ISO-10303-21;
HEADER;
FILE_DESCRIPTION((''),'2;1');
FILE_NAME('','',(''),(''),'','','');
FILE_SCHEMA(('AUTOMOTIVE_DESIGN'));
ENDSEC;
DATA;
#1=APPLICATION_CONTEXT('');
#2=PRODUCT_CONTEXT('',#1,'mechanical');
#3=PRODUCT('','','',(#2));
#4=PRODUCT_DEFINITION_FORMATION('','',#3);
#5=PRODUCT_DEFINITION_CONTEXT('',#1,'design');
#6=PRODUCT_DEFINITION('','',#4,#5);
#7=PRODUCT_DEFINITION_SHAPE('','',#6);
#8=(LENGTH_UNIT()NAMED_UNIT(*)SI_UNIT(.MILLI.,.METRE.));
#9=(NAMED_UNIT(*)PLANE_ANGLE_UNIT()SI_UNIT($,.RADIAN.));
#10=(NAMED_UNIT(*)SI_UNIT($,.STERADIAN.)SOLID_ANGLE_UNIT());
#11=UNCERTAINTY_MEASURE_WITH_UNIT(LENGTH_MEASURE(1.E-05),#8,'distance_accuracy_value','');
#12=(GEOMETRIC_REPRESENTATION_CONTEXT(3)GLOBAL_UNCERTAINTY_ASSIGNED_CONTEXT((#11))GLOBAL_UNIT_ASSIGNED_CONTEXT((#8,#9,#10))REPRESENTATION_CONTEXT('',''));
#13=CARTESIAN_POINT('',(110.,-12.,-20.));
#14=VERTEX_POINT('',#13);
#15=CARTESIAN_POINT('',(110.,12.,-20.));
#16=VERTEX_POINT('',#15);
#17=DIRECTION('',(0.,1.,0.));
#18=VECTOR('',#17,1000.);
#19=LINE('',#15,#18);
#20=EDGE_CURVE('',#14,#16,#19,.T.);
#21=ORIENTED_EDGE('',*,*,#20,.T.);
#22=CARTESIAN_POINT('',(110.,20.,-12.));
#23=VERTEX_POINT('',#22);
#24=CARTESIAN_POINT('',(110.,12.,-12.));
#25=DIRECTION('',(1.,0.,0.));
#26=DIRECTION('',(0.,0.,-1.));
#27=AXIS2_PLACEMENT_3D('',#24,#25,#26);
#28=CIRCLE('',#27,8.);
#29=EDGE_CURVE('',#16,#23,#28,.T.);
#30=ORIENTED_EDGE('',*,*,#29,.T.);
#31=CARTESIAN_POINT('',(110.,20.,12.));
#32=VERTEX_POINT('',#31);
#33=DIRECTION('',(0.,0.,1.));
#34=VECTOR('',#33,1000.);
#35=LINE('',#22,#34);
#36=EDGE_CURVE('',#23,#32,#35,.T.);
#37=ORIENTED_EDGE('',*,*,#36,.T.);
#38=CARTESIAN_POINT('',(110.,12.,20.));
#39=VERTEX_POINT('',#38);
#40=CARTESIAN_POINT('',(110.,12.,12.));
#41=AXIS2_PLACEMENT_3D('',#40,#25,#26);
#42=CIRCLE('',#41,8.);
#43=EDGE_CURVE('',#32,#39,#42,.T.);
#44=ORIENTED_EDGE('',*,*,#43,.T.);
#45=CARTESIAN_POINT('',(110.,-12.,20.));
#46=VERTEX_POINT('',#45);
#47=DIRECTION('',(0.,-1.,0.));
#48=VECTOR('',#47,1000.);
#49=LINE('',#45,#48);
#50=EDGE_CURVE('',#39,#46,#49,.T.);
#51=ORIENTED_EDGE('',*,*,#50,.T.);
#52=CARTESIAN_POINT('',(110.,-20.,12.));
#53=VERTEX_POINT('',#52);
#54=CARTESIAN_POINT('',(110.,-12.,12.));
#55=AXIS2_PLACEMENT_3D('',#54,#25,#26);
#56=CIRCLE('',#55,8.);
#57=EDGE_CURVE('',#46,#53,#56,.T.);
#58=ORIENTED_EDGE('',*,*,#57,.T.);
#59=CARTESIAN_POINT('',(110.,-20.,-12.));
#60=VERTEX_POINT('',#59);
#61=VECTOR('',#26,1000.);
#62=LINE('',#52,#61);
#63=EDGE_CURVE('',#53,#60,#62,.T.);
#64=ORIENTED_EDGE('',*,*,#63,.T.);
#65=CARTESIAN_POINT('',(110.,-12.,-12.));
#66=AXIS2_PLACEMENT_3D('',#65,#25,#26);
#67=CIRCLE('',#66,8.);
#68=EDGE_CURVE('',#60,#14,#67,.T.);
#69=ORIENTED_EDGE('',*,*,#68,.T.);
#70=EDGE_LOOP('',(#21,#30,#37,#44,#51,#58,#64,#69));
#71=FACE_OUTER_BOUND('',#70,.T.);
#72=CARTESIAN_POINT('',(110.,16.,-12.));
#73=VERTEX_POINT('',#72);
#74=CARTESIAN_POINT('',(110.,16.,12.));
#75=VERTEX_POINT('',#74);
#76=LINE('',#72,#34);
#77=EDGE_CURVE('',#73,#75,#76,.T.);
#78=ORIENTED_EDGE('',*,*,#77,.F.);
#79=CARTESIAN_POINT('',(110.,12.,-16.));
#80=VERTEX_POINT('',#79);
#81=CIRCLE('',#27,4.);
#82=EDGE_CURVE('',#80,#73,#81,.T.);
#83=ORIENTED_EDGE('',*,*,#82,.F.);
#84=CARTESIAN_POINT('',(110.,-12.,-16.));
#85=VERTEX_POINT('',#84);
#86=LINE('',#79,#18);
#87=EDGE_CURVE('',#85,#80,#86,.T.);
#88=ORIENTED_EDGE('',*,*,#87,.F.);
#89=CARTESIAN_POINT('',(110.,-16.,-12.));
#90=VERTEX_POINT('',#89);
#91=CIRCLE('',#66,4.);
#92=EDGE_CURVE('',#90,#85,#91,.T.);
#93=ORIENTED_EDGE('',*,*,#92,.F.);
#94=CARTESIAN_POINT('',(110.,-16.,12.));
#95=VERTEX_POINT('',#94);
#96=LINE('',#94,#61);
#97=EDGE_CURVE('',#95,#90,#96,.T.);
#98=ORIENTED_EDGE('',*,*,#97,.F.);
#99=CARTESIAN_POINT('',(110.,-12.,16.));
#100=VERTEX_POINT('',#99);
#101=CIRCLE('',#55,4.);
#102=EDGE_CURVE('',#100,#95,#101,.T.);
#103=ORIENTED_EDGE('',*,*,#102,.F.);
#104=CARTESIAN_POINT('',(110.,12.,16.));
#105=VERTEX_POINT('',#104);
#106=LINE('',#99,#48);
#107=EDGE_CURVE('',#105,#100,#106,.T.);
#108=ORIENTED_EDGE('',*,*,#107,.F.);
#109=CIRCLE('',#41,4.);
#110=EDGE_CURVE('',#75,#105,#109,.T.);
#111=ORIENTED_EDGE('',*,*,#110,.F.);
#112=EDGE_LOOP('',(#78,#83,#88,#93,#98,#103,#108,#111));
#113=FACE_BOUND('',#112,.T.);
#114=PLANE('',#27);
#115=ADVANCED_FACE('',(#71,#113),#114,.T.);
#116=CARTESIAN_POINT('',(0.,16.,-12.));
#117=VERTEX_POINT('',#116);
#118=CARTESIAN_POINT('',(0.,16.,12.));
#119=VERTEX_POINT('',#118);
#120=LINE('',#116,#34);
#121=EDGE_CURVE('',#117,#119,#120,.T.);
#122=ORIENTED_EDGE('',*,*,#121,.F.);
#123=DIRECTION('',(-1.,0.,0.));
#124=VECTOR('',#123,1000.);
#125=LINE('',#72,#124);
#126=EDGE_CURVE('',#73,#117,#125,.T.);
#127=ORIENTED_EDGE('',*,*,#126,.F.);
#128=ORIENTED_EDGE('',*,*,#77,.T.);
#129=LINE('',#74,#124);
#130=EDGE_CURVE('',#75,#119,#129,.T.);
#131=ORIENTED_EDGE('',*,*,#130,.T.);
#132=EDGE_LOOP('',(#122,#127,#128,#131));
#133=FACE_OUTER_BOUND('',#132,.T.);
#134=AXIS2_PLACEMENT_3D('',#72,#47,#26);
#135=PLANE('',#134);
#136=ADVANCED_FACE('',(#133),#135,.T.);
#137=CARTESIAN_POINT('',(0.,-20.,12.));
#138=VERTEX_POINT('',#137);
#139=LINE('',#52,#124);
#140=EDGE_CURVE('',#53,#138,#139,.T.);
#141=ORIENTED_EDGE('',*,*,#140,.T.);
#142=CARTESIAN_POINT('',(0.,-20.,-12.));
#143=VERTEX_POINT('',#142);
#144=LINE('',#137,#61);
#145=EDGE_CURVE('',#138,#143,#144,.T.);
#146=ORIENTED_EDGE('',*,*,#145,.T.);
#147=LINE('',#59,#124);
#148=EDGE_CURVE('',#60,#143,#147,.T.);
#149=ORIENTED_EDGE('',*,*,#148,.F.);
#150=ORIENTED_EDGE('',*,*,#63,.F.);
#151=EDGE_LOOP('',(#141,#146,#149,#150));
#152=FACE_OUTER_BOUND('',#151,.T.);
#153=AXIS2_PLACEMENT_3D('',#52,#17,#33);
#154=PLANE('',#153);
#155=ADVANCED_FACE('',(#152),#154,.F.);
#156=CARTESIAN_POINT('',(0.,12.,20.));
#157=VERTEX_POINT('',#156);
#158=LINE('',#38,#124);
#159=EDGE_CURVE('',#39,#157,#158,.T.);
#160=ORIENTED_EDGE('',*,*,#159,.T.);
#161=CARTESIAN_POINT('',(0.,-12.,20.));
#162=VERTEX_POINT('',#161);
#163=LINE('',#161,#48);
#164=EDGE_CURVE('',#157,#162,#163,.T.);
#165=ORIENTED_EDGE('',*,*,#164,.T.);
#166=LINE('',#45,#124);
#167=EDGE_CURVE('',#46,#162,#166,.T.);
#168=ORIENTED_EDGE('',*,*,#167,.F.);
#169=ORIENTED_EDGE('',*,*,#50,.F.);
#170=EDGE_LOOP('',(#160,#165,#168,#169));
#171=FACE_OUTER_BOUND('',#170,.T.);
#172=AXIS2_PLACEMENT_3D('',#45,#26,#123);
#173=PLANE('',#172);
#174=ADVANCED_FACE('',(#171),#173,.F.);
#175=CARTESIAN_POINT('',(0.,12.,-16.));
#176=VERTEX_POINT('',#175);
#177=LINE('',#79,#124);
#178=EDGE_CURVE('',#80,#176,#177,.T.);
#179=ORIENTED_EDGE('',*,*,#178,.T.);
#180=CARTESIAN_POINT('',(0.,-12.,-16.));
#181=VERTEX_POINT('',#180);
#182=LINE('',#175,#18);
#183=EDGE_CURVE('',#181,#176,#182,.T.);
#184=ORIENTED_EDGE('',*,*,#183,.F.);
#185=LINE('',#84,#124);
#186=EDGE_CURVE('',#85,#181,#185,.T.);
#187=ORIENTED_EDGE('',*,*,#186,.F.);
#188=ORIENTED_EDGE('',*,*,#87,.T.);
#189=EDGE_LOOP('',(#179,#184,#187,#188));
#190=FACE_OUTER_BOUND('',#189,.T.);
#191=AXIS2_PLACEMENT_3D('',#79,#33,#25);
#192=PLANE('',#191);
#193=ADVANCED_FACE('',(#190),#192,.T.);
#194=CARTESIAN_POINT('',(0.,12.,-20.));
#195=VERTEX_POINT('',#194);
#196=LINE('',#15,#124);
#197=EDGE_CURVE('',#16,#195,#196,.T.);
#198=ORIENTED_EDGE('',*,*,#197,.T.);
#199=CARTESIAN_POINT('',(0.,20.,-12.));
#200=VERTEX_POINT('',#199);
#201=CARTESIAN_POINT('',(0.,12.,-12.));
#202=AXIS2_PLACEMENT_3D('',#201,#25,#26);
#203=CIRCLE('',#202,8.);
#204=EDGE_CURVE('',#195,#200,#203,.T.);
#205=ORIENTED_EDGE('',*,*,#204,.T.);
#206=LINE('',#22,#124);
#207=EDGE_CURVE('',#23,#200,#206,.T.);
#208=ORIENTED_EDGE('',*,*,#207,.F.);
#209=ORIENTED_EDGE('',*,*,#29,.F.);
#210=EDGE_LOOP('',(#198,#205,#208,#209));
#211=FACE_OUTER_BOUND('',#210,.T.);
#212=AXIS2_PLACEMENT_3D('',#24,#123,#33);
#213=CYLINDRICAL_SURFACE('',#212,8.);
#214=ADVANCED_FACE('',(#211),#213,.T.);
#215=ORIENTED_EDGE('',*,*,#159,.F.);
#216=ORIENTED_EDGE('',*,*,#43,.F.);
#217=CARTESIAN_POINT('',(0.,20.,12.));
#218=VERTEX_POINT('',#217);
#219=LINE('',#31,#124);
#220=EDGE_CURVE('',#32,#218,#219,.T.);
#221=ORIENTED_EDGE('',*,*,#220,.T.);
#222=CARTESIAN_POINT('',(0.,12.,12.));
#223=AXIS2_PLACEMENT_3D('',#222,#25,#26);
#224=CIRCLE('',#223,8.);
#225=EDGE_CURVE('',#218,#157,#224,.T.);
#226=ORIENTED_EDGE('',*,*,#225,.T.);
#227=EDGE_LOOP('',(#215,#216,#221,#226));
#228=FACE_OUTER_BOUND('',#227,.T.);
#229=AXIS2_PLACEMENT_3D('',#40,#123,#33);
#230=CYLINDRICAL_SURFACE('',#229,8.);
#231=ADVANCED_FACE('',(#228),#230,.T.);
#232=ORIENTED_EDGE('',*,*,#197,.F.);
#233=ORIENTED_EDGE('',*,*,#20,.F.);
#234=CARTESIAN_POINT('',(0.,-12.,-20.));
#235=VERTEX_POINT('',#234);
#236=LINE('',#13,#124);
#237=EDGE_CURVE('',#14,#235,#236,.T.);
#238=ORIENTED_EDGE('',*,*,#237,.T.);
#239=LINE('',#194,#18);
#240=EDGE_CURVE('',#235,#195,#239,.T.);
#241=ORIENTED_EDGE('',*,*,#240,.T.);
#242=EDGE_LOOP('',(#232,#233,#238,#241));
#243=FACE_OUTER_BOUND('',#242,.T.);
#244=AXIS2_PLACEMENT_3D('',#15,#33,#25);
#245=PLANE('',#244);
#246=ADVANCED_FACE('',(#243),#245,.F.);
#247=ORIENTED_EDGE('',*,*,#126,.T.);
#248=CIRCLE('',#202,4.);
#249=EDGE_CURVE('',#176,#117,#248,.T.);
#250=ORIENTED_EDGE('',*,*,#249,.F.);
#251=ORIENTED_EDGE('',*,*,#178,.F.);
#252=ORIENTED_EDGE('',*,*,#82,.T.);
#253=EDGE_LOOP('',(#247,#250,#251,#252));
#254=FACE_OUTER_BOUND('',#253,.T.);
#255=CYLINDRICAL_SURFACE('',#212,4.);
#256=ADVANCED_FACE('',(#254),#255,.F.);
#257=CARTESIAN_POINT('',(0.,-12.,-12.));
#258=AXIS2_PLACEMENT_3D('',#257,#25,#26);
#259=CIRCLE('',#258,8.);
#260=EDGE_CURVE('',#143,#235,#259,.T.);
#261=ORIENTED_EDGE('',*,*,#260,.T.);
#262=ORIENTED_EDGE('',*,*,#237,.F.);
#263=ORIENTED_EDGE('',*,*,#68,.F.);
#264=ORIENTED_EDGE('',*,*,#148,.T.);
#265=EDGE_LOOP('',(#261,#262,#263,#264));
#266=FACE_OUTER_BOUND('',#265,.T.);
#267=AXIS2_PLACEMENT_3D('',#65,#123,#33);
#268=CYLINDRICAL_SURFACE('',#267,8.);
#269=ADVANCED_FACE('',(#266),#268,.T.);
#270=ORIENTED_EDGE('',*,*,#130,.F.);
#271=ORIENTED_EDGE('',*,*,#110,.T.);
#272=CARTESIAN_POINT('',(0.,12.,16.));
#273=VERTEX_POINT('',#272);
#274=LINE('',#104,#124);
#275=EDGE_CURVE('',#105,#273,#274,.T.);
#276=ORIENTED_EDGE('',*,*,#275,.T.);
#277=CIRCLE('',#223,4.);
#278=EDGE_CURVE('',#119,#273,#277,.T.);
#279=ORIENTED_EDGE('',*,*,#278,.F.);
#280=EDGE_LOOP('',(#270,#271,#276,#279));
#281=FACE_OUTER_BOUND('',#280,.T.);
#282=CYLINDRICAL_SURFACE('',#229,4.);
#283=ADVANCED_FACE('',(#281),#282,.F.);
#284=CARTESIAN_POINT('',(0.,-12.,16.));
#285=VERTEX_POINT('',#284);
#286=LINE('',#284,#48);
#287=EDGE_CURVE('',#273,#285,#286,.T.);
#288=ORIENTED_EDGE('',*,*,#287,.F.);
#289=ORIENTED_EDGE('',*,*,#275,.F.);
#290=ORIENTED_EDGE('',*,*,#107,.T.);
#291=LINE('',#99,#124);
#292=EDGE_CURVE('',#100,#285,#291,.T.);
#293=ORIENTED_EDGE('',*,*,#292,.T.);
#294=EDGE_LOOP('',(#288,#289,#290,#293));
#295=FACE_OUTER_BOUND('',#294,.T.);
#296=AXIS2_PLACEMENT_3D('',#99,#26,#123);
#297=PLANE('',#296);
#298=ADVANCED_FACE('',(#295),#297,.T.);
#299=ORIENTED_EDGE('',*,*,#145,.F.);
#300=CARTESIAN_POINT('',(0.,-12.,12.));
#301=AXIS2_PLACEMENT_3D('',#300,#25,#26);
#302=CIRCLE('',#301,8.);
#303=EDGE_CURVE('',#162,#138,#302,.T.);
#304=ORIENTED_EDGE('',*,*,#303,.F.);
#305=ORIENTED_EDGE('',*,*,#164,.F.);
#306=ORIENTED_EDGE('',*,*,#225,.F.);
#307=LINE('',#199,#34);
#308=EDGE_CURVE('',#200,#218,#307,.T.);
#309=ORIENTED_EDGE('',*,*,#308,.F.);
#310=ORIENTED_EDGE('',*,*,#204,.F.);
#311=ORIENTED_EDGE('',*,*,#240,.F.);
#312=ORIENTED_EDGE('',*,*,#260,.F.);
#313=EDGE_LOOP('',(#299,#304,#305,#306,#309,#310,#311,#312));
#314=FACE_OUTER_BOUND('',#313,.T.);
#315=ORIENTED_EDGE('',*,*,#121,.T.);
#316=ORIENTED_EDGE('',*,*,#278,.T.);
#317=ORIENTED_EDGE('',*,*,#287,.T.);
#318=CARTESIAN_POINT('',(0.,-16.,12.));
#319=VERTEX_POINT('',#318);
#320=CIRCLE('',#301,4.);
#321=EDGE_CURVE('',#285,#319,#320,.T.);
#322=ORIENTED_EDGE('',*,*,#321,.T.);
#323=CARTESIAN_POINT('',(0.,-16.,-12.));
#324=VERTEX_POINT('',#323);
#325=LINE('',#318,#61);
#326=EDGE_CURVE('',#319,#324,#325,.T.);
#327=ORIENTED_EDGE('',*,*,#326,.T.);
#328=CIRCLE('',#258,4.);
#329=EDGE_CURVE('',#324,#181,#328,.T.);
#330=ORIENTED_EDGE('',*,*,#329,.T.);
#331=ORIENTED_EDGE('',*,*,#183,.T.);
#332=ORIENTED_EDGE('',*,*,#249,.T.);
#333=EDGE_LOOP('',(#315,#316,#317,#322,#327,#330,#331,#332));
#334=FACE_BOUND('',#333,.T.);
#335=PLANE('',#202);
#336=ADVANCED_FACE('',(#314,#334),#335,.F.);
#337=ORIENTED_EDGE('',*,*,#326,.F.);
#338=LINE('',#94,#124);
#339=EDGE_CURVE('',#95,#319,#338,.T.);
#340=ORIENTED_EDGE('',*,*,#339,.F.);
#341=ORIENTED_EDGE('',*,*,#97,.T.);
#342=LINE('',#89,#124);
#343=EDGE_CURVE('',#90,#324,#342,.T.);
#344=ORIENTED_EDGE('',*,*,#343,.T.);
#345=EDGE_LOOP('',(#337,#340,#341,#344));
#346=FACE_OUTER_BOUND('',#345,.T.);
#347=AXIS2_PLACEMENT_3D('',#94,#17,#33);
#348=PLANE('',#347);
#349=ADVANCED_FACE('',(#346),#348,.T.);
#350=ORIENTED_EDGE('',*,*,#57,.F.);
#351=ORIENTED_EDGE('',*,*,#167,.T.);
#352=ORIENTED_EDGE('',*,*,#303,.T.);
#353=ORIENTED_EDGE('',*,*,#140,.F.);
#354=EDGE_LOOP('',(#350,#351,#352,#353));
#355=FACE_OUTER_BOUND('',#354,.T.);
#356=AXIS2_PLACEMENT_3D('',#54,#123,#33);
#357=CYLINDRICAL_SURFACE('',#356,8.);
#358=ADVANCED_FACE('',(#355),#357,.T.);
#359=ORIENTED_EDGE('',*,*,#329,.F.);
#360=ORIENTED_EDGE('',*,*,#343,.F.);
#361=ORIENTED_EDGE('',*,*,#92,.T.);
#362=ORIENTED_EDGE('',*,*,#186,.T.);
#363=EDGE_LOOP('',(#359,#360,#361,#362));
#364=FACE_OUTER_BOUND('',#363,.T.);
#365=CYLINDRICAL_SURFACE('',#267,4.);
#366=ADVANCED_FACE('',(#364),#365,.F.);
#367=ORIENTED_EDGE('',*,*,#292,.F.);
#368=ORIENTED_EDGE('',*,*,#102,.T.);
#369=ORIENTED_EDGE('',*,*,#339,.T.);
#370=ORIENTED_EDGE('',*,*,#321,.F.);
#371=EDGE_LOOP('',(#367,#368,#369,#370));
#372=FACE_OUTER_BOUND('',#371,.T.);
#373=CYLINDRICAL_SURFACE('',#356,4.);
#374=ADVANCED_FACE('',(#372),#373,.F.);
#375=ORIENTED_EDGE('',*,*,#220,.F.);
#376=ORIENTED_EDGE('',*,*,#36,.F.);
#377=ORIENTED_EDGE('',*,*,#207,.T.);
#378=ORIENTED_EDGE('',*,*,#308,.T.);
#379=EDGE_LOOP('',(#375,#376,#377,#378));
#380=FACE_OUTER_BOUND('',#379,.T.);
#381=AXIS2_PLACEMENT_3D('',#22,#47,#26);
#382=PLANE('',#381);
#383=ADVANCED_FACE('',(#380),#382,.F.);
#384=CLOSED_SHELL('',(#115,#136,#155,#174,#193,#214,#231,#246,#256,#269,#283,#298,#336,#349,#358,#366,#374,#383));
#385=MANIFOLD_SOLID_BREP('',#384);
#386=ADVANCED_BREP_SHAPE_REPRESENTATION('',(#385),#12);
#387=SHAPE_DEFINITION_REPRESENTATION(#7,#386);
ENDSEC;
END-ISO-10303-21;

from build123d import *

# Parameters (mm, degrees)
F_40_X_40_X_4_1_DEPTH = 110


with BuildPart() as part:
    # Sketch12 → 方形管 40 X 40 X 4(1) (new body)
    with BuildSketch(Plane(origin=(0, 0, 0), x_dir=(0, 0, -1), z_dir=(1, 0, 0))):
        with BuildLine():
            Line((-12, -20), (12, -20))
            ThreePointArc((12, -20), (17.656854249, -17.656854249), (20, -12))
            Line((20, -12), (20, 12))
            ThreePointArc((20, 12), (17.656854249, 17.656854249), (12, 20))
            Line((12, 20), (-12, 20))
            ThreePointArc((-12, 20), (-17.656854249, 17.656854249), (-20, 12))
            Line((-20, 12), (-20, -12))
            ThreePointArc((-20, -12), (-17.656854249, -17.656854249), (-12, -20))
        make_face()
        with BuildLine():
            Line((-12, -16), (12, -16))
            ThreePointArc((12, -16), (14.828427125, -14.828427125), (16, -12))
            Line((16, -12), (16, 12))
            ThreePointArc((16, 12), (14.828427125, 14.828427125), (12, 16))
            Line((12, 16), (-12, 16))
            ThreePointArc((-12, 16), (-14.828427125, 14.828427125), (-16, 12))
            Line((-16, 12), (-16, -12))
            ThreePointArc((-16, -12), (-14.828427125, -14.828427125), (-12, -16))
        make_face(mode=Mode.SUBTRACT)
    extrude(amount=F_40_X_40_X_4_1_DEPTH)


solid = part.part
